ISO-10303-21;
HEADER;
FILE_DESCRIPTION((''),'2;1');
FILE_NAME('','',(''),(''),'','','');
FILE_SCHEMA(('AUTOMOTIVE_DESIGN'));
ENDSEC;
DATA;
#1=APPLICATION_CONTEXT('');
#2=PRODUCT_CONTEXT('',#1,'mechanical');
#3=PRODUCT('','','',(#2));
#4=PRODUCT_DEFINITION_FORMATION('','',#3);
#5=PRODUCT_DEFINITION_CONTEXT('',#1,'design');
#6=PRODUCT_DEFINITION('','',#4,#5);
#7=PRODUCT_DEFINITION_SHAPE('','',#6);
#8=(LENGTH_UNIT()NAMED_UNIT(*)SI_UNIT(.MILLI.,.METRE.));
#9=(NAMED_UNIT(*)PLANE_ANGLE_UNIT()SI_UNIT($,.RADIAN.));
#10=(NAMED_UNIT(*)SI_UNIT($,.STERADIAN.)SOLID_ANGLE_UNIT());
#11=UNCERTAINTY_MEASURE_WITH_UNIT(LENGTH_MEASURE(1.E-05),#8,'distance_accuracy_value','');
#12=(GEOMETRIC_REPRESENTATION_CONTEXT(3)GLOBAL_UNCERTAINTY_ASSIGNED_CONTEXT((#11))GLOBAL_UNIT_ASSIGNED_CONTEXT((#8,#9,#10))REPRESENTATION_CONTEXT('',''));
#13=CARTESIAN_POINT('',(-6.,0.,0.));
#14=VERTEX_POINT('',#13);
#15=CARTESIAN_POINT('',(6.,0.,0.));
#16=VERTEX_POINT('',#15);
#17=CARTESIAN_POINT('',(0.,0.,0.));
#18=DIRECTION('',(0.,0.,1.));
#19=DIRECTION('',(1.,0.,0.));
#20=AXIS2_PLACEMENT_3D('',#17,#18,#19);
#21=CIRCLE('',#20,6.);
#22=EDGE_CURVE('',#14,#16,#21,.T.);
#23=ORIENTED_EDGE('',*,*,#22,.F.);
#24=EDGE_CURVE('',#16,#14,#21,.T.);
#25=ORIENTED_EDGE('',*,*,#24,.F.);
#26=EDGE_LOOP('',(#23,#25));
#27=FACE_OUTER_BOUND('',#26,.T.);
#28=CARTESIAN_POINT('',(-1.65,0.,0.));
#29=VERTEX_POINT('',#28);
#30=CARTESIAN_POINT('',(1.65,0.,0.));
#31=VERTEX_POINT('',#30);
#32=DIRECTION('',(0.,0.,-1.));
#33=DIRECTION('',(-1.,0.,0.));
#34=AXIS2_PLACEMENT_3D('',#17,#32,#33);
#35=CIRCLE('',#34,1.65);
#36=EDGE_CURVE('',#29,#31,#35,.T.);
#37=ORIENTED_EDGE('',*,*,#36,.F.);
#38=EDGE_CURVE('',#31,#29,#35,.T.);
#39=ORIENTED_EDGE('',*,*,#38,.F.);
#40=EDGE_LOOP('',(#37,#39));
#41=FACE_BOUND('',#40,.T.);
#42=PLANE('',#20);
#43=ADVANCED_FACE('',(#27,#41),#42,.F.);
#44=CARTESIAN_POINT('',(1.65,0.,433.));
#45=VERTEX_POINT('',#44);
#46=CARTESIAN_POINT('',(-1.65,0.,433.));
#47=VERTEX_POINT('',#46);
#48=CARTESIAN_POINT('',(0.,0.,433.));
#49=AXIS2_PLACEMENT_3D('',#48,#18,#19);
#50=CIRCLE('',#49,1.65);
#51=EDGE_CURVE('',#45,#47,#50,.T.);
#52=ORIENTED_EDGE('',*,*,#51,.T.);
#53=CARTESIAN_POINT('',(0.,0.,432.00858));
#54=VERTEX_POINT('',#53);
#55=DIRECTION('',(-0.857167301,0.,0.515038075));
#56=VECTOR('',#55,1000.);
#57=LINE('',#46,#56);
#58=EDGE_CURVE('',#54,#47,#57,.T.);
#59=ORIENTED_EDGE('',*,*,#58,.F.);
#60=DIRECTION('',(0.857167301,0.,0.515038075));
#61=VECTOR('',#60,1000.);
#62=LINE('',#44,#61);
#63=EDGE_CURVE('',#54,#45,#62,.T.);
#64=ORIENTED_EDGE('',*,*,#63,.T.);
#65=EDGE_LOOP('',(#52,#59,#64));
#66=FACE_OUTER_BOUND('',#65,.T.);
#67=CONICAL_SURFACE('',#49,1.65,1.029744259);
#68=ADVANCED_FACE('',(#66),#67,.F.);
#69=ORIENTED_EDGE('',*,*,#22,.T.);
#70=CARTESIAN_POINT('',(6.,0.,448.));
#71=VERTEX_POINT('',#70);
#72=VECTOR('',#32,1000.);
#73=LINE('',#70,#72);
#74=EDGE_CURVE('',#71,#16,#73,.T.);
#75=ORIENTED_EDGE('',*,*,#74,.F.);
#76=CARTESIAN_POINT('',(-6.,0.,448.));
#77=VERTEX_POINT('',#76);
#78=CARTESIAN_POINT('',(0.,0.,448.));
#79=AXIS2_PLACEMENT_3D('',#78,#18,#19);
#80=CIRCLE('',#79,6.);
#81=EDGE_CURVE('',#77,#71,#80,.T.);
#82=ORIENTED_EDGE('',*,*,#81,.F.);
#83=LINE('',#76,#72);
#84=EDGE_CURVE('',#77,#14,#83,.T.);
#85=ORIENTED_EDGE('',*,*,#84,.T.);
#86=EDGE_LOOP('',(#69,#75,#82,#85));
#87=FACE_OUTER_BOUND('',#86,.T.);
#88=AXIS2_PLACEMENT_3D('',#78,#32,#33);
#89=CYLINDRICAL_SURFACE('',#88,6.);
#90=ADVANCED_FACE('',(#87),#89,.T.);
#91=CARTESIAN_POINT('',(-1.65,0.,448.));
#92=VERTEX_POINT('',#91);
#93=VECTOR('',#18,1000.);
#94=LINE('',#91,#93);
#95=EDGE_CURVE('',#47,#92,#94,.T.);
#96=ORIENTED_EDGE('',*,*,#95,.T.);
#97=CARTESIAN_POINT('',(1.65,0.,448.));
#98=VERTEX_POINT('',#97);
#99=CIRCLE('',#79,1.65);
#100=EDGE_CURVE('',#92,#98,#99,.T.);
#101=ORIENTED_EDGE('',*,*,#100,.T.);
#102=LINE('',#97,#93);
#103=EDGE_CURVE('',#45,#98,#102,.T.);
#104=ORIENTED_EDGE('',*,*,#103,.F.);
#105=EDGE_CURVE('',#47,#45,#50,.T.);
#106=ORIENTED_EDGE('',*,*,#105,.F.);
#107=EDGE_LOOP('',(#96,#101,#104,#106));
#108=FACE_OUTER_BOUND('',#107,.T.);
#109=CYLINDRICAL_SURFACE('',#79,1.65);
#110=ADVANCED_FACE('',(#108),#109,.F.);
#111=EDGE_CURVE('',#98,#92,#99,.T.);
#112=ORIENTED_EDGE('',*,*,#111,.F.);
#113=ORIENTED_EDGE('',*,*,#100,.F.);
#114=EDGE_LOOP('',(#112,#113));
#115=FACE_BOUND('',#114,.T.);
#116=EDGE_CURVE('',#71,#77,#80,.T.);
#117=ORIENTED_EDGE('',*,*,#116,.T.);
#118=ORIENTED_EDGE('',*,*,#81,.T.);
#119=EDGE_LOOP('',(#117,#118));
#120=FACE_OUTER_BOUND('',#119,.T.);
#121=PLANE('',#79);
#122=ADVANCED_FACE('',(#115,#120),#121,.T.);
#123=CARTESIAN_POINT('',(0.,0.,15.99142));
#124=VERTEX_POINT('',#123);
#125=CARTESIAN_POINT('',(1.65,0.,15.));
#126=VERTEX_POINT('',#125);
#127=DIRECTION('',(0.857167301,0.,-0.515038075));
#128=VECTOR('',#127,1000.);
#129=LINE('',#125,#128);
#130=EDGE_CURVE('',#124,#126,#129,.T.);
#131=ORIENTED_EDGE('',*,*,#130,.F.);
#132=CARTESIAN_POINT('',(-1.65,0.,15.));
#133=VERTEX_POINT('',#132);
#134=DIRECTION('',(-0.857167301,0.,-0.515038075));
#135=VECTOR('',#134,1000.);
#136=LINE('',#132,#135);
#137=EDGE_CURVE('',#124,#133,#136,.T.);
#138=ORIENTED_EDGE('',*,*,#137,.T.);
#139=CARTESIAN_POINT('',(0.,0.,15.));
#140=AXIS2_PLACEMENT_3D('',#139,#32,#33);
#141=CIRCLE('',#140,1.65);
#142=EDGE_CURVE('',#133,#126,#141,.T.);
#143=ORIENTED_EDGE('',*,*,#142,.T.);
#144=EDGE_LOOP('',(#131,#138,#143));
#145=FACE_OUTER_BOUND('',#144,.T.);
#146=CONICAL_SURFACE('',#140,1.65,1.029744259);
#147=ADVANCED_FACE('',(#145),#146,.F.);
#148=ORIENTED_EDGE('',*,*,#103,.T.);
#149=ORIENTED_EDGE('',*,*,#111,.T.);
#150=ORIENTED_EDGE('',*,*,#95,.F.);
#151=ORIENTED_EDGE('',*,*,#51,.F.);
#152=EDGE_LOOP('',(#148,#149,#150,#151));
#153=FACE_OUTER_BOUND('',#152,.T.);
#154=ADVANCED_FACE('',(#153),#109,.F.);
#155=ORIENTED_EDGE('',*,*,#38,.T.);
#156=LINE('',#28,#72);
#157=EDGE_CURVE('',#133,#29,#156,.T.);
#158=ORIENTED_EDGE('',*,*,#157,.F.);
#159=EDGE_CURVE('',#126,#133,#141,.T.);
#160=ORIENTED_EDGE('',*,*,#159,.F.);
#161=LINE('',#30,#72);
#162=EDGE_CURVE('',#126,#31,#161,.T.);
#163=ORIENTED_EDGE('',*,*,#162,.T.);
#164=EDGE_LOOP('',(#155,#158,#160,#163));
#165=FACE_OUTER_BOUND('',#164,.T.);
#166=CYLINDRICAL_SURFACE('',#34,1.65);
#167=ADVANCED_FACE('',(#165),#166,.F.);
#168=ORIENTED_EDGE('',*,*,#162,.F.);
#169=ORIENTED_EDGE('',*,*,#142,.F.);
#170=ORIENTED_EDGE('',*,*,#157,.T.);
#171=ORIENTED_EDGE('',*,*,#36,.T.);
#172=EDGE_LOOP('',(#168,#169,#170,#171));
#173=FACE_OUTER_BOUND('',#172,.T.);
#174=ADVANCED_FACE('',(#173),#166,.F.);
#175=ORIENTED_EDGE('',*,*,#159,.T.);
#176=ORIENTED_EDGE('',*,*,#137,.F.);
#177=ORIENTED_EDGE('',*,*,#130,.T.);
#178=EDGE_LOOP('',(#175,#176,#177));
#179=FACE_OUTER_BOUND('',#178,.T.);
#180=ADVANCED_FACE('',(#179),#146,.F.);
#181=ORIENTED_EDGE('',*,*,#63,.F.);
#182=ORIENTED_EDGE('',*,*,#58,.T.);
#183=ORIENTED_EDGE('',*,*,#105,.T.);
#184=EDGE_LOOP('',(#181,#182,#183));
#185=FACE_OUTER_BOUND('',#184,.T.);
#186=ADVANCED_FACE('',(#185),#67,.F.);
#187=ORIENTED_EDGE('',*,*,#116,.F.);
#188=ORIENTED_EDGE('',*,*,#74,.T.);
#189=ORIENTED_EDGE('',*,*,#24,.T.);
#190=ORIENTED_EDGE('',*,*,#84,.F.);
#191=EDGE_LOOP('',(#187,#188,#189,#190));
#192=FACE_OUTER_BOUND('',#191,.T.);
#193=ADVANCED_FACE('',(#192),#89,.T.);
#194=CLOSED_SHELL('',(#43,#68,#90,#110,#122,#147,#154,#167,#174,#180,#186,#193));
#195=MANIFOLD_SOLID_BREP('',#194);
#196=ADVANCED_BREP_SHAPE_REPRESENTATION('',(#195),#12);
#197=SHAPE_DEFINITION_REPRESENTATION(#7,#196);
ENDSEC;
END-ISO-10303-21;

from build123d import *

# Parameters (mm, degrees)
SKETCH_1_R             = 6
EXTRUDE_1_DEPTH        = 448
HOLE_WIZARD_M4_1_D     = 3.3
HOLE_WIZARD_M4_1_DEPTH = 15
HOLE_WIZARD_M4_1_TIP   = 0.991420021
HOLE_WIZARD_M4_2_D     = 3.3
HOLE_WIZARD_M4_2_DEPTH = 15
HOLE_WIZARD_M4_2_TIP   = 0.991420021


with BuildPart() as part:
    # 草图1 → 凸台-拉伸1 (new body)
    with BuildSketch(Plane.XY):
        Circle(SKETCH_1_R)
    extrude(amount=EXTRUDE_1_DEPTH)

    # M4 螺纹孔1
    with Locations(Plane(origin=(0, 0, 0), x_dir=(-1, 0, 0), z_dir=(0, 0, -1))):
        with Locations((0, 0)):
            Hole(HOLE_WIZARD_M4_1_D / 2, depth=HOLE_WIZARD_M4_1_DEPTH)
            with Locations((0, 0, -(HOLE_WIZARD_M4_1_DEPTH + HOLE_WIZARD_M4_1_TIP / 2))):  # 118° drill point
                Cone(0, HOLE_WIZARD_M4_1_D / 2, HOLE_WIZARD_M4_1_TIP, mode=Mode.SUBTRACT)

    # M4 螺纹孔2
    with Locations(Plane.XY.offset(448)):
        with Locations((0, 0)):
            Hole(HOLE_WIZARD_M4_2_D / 2, depth=HOLE_WIZARD_M4_2_DEPTH)
            with Locations((0, 0, -(HOLE_WIZARD_M4_2_DEPTH + HOLE_WIZARD_M4_2_TIP / 2))):  # 118° drill point
                Cone(0, HOLE_WIZARD_M4_2_D / 2, HOLE_WIZARD_M4_2_TIP, mode=Mode.SUBTRACT)


solid = part.part
